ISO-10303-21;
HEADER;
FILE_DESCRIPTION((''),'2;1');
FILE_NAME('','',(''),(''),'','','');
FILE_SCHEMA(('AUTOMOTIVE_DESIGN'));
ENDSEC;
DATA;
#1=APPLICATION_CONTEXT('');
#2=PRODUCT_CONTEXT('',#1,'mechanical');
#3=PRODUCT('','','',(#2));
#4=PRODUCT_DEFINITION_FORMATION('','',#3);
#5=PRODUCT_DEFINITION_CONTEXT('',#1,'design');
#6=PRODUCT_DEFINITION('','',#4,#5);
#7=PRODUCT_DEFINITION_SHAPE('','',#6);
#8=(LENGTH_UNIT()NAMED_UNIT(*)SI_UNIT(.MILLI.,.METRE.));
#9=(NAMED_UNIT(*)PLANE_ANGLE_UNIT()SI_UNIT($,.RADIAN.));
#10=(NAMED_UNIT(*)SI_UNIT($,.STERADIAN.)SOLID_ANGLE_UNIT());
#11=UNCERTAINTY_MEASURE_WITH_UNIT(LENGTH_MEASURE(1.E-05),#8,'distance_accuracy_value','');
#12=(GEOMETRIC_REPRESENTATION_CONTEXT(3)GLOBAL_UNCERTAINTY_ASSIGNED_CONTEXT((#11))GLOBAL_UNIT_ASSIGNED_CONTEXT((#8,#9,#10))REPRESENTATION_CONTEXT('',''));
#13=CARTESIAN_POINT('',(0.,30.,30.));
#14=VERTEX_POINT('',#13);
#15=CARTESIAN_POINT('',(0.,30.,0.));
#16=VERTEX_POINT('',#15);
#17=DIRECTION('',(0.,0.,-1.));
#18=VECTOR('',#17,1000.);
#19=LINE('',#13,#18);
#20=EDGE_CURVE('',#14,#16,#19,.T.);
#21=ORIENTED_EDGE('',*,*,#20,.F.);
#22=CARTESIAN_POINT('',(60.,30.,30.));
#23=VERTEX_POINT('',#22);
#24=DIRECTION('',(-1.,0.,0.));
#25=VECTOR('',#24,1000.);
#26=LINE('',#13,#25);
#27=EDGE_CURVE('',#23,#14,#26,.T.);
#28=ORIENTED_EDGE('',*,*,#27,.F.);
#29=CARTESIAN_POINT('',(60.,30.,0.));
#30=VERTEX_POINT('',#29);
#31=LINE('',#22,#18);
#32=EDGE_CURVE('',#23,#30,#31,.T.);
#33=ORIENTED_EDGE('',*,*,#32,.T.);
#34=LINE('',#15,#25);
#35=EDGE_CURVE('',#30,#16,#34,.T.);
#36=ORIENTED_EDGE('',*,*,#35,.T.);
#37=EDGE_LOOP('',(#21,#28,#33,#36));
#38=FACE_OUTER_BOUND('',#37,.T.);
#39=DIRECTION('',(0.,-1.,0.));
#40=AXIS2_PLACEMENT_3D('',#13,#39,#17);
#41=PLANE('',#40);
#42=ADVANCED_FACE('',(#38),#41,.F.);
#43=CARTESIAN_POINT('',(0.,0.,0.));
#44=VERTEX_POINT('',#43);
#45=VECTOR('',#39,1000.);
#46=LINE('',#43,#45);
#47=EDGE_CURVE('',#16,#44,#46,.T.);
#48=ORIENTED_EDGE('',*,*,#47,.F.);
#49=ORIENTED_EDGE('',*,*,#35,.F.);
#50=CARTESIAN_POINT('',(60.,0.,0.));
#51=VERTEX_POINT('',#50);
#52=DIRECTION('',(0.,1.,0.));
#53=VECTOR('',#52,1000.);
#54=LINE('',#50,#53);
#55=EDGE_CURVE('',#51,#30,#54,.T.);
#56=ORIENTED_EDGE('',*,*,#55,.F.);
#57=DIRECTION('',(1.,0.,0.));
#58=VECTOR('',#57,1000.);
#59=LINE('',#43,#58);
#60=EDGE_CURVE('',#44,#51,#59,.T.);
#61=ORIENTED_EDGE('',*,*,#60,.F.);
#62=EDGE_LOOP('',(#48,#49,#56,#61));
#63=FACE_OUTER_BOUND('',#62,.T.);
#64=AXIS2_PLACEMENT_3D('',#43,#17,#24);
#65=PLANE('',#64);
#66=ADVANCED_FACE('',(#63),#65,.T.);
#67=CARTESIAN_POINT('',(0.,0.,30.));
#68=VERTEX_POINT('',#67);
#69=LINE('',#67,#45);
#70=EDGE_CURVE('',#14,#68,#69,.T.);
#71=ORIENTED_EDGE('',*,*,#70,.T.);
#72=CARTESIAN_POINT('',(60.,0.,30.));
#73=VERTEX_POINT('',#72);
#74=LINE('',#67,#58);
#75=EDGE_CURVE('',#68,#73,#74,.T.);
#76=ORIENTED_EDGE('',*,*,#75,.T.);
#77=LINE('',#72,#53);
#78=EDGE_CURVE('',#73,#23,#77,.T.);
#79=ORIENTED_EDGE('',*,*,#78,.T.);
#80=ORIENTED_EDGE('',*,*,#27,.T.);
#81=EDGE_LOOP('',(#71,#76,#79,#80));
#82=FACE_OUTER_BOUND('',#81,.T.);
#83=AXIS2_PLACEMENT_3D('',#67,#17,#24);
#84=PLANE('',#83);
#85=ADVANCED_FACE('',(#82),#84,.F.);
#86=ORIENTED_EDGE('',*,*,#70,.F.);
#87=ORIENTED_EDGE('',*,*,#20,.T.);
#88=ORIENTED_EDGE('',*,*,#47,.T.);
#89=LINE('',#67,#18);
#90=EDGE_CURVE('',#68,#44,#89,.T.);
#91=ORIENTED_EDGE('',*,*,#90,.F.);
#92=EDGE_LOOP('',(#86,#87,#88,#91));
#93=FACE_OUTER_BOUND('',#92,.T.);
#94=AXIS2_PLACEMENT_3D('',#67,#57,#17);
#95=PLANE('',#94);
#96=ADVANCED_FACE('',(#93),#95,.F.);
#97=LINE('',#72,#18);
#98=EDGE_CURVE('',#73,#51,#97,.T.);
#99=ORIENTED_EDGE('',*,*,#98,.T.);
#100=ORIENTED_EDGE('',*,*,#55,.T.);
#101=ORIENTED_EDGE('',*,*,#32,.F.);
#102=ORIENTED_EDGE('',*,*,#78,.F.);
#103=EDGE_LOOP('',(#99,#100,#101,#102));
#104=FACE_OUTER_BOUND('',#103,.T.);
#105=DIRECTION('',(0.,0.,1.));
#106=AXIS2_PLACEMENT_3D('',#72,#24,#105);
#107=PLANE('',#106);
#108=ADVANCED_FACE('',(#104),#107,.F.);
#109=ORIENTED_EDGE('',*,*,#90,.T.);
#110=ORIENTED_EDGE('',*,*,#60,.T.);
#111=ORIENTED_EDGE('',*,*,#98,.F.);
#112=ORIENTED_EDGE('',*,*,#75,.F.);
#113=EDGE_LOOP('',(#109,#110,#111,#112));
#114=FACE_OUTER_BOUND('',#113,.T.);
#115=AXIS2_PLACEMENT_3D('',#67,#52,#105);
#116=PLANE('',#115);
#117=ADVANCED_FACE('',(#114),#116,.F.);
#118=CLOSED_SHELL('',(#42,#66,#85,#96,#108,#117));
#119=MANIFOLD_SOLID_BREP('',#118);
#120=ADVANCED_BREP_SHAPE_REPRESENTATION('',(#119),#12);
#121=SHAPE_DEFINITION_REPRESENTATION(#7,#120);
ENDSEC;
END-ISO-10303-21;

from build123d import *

# Parameters (mm, degrees)
SKETCH1_W           = 60
SKETCH1_H           = 30
BOSS_EXTRUDE1_DEPTH = 30


with BuildPart() as part:
    # Sketch1 → Boss-Extrude1 (new body)
    with BuildSketch(Plane.XY):
        with Locations((30, 15)):
            Rectangle(SKETCH1_W, SKETCH1_H)
    extrude(amount=BOSS_EXTRUDE1_DEPTH)


solid = part.part
